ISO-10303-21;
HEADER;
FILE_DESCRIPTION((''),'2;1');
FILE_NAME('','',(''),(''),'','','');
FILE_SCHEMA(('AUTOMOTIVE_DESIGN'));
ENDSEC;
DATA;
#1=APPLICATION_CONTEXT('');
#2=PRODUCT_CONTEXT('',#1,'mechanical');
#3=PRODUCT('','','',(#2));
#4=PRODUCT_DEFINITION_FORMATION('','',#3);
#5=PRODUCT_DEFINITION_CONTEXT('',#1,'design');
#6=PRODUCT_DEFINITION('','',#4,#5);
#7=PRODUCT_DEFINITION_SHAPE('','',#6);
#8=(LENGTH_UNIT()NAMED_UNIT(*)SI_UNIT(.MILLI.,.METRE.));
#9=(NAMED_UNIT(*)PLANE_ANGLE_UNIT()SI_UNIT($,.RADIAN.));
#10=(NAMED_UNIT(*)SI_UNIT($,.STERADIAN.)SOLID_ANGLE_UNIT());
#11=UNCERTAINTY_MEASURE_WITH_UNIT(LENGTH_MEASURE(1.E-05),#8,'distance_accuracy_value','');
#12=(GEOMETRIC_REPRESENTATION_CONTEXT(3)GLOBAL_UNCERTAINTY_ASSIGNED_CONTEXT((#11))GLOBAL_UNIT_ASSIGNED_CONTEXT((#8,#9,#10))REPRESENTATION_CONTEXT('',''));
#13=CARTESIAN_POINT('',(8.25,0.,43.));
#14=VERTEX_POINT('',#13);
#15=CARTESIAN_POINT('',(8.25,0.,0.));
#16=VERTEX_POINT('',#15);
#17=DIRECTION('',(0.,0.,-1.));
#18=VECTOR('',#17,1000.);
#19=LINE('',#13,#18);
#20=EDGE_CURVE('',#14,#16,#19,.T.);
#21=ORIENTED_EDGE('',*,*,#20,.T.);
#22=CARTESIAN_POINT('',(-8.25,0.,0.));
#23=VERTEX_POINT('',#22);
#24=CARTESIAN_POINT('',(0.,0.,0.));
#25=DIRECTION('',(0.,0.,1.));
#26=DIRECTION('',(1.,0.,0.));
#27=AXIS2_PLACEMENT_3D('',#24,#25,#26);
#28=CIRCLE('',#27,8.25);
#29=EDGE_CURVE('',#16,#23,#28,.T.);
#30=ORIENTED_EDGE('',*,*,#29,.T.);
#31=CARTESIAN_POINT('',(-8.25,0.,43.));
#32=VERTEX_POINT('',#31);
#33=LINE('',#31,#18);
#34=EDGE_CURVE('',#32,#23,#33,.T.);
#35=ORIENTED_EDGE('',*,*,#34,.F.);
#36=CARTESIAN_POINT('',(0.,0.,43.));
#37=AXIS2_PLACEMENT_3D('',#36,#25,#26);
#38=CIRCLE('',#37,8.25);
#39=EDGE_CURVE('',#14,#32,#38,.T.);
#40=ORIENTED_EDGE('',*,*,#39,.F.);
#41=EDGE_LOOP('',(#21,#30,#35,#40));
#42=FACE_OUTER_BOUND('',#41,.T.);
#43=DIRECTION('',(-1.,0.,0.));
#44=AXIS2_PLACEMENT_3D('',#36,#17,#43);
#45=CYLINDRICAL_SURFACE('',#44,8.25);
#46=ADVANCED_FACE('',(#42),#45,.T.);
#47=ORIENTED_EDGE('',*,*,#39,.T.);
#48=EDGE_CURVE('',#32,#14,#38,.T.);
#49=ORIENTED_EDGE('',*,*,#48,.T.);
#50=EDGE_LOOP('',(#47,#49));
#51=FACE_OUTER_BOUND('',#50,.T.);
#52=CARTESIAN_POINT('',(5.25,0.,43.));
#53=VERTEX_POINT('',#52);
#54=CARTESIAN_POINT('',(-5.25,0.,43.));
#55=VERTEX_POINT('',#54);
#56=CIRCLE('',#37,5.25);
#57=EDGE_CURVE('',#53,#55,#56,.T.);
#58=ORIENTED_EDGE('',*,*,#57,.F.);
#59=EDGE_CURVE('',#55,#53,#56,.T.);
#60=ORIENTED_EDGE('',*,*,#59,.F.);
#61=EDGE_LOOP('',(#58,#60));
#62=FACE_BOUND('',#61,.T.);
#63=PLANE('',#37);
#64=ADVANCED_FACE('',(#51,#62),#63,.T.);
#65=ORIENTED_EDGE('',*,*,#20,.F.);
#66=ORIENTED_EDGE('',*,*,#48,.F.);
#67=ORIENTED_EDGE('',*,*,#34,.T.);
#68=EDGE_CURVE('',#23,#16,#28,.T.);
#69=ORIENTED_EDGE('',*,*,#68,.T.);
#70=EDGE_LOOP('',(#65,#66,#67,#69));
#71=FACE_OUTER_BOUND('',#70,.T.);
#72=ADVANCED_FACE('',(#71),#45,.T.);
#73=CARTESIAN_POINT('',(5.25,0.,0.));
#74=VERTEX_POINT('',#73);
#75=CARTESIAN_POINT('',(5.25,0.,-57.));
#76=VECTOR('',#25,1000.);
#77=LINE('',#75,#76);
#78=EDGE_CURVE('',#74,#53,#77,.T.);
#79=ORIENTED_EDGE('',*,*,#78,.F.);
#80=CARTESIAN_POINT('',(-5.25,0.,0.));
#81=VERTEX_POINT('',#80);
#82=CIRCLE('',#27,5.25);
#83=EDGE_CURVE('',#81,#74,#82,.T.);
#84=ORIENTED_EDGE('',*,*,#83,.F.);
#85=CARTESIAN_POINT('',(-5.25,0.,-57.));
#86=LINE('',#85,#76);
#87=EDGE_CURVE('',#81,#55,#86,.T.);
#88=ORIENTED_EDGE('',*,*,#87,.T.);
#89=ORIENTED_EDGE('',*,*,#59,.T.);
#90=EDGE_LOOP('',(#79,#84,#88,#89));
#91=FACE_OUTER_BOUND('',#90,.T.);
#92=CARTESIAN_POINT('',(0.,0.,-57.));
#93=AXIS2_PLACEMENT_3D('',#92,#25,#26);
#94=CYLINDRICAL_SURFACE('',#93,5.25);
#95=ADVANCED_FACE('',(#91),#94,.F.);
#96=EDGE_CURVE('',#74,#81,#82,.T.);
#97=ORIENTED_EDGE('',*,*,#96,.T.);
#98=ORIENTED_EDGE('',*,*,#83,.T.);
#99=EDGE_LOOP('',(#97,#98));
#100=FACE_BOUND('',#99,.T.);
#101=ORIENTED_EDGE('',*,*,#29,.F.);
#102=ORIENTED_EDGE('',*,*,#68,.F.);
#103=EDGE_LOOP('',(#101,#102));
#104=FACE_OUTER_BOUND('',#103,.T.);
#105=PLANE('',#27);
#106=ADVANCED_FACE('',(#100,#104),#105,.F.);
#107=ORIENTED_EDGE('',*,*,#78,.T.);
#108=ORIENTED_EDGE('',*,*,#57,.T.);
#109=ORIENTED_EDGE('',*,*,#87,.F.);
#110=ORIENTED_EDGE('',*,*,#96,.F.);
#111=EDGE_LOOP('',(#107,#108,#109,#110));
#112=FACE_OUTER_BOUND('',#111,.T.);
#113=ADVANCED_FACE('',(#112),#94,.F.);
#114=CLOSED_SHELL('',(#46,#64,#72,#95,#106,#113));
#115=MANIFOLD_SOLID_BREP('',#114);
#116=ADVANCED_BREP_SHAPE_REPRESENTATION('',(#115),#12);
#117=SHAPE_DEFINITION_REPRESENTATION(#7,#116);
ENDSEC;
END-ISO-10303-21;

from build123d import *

# Parameters (mm, degrees)
SKETCH1_R           = 8.25
BOSS_EXTRUDE1_DEPTH = 43
SKETCH2_R           = 5.25
CUT_EXTRUDE1_DEPTH  = 100


with BuildPart() as part:
    # Sketch1 → Boss-Extrude1 (new body)
    with BuildSketch(Plane.XY):
        Circle(SKETCH1_R)
    extrude(amount=BOSS_EXTRUDE1_DEPTH)

    # Sketch2 → Cut-Extrude1 (cut)
    with BuildSketch(Plane.XY.offset(43)):
        Circle(SKETCH2_R)
    extrude(amount=-CUT_EXTRUDE1_DEPTH, mode=Mode.SUBTRACT)


solid = part.part
